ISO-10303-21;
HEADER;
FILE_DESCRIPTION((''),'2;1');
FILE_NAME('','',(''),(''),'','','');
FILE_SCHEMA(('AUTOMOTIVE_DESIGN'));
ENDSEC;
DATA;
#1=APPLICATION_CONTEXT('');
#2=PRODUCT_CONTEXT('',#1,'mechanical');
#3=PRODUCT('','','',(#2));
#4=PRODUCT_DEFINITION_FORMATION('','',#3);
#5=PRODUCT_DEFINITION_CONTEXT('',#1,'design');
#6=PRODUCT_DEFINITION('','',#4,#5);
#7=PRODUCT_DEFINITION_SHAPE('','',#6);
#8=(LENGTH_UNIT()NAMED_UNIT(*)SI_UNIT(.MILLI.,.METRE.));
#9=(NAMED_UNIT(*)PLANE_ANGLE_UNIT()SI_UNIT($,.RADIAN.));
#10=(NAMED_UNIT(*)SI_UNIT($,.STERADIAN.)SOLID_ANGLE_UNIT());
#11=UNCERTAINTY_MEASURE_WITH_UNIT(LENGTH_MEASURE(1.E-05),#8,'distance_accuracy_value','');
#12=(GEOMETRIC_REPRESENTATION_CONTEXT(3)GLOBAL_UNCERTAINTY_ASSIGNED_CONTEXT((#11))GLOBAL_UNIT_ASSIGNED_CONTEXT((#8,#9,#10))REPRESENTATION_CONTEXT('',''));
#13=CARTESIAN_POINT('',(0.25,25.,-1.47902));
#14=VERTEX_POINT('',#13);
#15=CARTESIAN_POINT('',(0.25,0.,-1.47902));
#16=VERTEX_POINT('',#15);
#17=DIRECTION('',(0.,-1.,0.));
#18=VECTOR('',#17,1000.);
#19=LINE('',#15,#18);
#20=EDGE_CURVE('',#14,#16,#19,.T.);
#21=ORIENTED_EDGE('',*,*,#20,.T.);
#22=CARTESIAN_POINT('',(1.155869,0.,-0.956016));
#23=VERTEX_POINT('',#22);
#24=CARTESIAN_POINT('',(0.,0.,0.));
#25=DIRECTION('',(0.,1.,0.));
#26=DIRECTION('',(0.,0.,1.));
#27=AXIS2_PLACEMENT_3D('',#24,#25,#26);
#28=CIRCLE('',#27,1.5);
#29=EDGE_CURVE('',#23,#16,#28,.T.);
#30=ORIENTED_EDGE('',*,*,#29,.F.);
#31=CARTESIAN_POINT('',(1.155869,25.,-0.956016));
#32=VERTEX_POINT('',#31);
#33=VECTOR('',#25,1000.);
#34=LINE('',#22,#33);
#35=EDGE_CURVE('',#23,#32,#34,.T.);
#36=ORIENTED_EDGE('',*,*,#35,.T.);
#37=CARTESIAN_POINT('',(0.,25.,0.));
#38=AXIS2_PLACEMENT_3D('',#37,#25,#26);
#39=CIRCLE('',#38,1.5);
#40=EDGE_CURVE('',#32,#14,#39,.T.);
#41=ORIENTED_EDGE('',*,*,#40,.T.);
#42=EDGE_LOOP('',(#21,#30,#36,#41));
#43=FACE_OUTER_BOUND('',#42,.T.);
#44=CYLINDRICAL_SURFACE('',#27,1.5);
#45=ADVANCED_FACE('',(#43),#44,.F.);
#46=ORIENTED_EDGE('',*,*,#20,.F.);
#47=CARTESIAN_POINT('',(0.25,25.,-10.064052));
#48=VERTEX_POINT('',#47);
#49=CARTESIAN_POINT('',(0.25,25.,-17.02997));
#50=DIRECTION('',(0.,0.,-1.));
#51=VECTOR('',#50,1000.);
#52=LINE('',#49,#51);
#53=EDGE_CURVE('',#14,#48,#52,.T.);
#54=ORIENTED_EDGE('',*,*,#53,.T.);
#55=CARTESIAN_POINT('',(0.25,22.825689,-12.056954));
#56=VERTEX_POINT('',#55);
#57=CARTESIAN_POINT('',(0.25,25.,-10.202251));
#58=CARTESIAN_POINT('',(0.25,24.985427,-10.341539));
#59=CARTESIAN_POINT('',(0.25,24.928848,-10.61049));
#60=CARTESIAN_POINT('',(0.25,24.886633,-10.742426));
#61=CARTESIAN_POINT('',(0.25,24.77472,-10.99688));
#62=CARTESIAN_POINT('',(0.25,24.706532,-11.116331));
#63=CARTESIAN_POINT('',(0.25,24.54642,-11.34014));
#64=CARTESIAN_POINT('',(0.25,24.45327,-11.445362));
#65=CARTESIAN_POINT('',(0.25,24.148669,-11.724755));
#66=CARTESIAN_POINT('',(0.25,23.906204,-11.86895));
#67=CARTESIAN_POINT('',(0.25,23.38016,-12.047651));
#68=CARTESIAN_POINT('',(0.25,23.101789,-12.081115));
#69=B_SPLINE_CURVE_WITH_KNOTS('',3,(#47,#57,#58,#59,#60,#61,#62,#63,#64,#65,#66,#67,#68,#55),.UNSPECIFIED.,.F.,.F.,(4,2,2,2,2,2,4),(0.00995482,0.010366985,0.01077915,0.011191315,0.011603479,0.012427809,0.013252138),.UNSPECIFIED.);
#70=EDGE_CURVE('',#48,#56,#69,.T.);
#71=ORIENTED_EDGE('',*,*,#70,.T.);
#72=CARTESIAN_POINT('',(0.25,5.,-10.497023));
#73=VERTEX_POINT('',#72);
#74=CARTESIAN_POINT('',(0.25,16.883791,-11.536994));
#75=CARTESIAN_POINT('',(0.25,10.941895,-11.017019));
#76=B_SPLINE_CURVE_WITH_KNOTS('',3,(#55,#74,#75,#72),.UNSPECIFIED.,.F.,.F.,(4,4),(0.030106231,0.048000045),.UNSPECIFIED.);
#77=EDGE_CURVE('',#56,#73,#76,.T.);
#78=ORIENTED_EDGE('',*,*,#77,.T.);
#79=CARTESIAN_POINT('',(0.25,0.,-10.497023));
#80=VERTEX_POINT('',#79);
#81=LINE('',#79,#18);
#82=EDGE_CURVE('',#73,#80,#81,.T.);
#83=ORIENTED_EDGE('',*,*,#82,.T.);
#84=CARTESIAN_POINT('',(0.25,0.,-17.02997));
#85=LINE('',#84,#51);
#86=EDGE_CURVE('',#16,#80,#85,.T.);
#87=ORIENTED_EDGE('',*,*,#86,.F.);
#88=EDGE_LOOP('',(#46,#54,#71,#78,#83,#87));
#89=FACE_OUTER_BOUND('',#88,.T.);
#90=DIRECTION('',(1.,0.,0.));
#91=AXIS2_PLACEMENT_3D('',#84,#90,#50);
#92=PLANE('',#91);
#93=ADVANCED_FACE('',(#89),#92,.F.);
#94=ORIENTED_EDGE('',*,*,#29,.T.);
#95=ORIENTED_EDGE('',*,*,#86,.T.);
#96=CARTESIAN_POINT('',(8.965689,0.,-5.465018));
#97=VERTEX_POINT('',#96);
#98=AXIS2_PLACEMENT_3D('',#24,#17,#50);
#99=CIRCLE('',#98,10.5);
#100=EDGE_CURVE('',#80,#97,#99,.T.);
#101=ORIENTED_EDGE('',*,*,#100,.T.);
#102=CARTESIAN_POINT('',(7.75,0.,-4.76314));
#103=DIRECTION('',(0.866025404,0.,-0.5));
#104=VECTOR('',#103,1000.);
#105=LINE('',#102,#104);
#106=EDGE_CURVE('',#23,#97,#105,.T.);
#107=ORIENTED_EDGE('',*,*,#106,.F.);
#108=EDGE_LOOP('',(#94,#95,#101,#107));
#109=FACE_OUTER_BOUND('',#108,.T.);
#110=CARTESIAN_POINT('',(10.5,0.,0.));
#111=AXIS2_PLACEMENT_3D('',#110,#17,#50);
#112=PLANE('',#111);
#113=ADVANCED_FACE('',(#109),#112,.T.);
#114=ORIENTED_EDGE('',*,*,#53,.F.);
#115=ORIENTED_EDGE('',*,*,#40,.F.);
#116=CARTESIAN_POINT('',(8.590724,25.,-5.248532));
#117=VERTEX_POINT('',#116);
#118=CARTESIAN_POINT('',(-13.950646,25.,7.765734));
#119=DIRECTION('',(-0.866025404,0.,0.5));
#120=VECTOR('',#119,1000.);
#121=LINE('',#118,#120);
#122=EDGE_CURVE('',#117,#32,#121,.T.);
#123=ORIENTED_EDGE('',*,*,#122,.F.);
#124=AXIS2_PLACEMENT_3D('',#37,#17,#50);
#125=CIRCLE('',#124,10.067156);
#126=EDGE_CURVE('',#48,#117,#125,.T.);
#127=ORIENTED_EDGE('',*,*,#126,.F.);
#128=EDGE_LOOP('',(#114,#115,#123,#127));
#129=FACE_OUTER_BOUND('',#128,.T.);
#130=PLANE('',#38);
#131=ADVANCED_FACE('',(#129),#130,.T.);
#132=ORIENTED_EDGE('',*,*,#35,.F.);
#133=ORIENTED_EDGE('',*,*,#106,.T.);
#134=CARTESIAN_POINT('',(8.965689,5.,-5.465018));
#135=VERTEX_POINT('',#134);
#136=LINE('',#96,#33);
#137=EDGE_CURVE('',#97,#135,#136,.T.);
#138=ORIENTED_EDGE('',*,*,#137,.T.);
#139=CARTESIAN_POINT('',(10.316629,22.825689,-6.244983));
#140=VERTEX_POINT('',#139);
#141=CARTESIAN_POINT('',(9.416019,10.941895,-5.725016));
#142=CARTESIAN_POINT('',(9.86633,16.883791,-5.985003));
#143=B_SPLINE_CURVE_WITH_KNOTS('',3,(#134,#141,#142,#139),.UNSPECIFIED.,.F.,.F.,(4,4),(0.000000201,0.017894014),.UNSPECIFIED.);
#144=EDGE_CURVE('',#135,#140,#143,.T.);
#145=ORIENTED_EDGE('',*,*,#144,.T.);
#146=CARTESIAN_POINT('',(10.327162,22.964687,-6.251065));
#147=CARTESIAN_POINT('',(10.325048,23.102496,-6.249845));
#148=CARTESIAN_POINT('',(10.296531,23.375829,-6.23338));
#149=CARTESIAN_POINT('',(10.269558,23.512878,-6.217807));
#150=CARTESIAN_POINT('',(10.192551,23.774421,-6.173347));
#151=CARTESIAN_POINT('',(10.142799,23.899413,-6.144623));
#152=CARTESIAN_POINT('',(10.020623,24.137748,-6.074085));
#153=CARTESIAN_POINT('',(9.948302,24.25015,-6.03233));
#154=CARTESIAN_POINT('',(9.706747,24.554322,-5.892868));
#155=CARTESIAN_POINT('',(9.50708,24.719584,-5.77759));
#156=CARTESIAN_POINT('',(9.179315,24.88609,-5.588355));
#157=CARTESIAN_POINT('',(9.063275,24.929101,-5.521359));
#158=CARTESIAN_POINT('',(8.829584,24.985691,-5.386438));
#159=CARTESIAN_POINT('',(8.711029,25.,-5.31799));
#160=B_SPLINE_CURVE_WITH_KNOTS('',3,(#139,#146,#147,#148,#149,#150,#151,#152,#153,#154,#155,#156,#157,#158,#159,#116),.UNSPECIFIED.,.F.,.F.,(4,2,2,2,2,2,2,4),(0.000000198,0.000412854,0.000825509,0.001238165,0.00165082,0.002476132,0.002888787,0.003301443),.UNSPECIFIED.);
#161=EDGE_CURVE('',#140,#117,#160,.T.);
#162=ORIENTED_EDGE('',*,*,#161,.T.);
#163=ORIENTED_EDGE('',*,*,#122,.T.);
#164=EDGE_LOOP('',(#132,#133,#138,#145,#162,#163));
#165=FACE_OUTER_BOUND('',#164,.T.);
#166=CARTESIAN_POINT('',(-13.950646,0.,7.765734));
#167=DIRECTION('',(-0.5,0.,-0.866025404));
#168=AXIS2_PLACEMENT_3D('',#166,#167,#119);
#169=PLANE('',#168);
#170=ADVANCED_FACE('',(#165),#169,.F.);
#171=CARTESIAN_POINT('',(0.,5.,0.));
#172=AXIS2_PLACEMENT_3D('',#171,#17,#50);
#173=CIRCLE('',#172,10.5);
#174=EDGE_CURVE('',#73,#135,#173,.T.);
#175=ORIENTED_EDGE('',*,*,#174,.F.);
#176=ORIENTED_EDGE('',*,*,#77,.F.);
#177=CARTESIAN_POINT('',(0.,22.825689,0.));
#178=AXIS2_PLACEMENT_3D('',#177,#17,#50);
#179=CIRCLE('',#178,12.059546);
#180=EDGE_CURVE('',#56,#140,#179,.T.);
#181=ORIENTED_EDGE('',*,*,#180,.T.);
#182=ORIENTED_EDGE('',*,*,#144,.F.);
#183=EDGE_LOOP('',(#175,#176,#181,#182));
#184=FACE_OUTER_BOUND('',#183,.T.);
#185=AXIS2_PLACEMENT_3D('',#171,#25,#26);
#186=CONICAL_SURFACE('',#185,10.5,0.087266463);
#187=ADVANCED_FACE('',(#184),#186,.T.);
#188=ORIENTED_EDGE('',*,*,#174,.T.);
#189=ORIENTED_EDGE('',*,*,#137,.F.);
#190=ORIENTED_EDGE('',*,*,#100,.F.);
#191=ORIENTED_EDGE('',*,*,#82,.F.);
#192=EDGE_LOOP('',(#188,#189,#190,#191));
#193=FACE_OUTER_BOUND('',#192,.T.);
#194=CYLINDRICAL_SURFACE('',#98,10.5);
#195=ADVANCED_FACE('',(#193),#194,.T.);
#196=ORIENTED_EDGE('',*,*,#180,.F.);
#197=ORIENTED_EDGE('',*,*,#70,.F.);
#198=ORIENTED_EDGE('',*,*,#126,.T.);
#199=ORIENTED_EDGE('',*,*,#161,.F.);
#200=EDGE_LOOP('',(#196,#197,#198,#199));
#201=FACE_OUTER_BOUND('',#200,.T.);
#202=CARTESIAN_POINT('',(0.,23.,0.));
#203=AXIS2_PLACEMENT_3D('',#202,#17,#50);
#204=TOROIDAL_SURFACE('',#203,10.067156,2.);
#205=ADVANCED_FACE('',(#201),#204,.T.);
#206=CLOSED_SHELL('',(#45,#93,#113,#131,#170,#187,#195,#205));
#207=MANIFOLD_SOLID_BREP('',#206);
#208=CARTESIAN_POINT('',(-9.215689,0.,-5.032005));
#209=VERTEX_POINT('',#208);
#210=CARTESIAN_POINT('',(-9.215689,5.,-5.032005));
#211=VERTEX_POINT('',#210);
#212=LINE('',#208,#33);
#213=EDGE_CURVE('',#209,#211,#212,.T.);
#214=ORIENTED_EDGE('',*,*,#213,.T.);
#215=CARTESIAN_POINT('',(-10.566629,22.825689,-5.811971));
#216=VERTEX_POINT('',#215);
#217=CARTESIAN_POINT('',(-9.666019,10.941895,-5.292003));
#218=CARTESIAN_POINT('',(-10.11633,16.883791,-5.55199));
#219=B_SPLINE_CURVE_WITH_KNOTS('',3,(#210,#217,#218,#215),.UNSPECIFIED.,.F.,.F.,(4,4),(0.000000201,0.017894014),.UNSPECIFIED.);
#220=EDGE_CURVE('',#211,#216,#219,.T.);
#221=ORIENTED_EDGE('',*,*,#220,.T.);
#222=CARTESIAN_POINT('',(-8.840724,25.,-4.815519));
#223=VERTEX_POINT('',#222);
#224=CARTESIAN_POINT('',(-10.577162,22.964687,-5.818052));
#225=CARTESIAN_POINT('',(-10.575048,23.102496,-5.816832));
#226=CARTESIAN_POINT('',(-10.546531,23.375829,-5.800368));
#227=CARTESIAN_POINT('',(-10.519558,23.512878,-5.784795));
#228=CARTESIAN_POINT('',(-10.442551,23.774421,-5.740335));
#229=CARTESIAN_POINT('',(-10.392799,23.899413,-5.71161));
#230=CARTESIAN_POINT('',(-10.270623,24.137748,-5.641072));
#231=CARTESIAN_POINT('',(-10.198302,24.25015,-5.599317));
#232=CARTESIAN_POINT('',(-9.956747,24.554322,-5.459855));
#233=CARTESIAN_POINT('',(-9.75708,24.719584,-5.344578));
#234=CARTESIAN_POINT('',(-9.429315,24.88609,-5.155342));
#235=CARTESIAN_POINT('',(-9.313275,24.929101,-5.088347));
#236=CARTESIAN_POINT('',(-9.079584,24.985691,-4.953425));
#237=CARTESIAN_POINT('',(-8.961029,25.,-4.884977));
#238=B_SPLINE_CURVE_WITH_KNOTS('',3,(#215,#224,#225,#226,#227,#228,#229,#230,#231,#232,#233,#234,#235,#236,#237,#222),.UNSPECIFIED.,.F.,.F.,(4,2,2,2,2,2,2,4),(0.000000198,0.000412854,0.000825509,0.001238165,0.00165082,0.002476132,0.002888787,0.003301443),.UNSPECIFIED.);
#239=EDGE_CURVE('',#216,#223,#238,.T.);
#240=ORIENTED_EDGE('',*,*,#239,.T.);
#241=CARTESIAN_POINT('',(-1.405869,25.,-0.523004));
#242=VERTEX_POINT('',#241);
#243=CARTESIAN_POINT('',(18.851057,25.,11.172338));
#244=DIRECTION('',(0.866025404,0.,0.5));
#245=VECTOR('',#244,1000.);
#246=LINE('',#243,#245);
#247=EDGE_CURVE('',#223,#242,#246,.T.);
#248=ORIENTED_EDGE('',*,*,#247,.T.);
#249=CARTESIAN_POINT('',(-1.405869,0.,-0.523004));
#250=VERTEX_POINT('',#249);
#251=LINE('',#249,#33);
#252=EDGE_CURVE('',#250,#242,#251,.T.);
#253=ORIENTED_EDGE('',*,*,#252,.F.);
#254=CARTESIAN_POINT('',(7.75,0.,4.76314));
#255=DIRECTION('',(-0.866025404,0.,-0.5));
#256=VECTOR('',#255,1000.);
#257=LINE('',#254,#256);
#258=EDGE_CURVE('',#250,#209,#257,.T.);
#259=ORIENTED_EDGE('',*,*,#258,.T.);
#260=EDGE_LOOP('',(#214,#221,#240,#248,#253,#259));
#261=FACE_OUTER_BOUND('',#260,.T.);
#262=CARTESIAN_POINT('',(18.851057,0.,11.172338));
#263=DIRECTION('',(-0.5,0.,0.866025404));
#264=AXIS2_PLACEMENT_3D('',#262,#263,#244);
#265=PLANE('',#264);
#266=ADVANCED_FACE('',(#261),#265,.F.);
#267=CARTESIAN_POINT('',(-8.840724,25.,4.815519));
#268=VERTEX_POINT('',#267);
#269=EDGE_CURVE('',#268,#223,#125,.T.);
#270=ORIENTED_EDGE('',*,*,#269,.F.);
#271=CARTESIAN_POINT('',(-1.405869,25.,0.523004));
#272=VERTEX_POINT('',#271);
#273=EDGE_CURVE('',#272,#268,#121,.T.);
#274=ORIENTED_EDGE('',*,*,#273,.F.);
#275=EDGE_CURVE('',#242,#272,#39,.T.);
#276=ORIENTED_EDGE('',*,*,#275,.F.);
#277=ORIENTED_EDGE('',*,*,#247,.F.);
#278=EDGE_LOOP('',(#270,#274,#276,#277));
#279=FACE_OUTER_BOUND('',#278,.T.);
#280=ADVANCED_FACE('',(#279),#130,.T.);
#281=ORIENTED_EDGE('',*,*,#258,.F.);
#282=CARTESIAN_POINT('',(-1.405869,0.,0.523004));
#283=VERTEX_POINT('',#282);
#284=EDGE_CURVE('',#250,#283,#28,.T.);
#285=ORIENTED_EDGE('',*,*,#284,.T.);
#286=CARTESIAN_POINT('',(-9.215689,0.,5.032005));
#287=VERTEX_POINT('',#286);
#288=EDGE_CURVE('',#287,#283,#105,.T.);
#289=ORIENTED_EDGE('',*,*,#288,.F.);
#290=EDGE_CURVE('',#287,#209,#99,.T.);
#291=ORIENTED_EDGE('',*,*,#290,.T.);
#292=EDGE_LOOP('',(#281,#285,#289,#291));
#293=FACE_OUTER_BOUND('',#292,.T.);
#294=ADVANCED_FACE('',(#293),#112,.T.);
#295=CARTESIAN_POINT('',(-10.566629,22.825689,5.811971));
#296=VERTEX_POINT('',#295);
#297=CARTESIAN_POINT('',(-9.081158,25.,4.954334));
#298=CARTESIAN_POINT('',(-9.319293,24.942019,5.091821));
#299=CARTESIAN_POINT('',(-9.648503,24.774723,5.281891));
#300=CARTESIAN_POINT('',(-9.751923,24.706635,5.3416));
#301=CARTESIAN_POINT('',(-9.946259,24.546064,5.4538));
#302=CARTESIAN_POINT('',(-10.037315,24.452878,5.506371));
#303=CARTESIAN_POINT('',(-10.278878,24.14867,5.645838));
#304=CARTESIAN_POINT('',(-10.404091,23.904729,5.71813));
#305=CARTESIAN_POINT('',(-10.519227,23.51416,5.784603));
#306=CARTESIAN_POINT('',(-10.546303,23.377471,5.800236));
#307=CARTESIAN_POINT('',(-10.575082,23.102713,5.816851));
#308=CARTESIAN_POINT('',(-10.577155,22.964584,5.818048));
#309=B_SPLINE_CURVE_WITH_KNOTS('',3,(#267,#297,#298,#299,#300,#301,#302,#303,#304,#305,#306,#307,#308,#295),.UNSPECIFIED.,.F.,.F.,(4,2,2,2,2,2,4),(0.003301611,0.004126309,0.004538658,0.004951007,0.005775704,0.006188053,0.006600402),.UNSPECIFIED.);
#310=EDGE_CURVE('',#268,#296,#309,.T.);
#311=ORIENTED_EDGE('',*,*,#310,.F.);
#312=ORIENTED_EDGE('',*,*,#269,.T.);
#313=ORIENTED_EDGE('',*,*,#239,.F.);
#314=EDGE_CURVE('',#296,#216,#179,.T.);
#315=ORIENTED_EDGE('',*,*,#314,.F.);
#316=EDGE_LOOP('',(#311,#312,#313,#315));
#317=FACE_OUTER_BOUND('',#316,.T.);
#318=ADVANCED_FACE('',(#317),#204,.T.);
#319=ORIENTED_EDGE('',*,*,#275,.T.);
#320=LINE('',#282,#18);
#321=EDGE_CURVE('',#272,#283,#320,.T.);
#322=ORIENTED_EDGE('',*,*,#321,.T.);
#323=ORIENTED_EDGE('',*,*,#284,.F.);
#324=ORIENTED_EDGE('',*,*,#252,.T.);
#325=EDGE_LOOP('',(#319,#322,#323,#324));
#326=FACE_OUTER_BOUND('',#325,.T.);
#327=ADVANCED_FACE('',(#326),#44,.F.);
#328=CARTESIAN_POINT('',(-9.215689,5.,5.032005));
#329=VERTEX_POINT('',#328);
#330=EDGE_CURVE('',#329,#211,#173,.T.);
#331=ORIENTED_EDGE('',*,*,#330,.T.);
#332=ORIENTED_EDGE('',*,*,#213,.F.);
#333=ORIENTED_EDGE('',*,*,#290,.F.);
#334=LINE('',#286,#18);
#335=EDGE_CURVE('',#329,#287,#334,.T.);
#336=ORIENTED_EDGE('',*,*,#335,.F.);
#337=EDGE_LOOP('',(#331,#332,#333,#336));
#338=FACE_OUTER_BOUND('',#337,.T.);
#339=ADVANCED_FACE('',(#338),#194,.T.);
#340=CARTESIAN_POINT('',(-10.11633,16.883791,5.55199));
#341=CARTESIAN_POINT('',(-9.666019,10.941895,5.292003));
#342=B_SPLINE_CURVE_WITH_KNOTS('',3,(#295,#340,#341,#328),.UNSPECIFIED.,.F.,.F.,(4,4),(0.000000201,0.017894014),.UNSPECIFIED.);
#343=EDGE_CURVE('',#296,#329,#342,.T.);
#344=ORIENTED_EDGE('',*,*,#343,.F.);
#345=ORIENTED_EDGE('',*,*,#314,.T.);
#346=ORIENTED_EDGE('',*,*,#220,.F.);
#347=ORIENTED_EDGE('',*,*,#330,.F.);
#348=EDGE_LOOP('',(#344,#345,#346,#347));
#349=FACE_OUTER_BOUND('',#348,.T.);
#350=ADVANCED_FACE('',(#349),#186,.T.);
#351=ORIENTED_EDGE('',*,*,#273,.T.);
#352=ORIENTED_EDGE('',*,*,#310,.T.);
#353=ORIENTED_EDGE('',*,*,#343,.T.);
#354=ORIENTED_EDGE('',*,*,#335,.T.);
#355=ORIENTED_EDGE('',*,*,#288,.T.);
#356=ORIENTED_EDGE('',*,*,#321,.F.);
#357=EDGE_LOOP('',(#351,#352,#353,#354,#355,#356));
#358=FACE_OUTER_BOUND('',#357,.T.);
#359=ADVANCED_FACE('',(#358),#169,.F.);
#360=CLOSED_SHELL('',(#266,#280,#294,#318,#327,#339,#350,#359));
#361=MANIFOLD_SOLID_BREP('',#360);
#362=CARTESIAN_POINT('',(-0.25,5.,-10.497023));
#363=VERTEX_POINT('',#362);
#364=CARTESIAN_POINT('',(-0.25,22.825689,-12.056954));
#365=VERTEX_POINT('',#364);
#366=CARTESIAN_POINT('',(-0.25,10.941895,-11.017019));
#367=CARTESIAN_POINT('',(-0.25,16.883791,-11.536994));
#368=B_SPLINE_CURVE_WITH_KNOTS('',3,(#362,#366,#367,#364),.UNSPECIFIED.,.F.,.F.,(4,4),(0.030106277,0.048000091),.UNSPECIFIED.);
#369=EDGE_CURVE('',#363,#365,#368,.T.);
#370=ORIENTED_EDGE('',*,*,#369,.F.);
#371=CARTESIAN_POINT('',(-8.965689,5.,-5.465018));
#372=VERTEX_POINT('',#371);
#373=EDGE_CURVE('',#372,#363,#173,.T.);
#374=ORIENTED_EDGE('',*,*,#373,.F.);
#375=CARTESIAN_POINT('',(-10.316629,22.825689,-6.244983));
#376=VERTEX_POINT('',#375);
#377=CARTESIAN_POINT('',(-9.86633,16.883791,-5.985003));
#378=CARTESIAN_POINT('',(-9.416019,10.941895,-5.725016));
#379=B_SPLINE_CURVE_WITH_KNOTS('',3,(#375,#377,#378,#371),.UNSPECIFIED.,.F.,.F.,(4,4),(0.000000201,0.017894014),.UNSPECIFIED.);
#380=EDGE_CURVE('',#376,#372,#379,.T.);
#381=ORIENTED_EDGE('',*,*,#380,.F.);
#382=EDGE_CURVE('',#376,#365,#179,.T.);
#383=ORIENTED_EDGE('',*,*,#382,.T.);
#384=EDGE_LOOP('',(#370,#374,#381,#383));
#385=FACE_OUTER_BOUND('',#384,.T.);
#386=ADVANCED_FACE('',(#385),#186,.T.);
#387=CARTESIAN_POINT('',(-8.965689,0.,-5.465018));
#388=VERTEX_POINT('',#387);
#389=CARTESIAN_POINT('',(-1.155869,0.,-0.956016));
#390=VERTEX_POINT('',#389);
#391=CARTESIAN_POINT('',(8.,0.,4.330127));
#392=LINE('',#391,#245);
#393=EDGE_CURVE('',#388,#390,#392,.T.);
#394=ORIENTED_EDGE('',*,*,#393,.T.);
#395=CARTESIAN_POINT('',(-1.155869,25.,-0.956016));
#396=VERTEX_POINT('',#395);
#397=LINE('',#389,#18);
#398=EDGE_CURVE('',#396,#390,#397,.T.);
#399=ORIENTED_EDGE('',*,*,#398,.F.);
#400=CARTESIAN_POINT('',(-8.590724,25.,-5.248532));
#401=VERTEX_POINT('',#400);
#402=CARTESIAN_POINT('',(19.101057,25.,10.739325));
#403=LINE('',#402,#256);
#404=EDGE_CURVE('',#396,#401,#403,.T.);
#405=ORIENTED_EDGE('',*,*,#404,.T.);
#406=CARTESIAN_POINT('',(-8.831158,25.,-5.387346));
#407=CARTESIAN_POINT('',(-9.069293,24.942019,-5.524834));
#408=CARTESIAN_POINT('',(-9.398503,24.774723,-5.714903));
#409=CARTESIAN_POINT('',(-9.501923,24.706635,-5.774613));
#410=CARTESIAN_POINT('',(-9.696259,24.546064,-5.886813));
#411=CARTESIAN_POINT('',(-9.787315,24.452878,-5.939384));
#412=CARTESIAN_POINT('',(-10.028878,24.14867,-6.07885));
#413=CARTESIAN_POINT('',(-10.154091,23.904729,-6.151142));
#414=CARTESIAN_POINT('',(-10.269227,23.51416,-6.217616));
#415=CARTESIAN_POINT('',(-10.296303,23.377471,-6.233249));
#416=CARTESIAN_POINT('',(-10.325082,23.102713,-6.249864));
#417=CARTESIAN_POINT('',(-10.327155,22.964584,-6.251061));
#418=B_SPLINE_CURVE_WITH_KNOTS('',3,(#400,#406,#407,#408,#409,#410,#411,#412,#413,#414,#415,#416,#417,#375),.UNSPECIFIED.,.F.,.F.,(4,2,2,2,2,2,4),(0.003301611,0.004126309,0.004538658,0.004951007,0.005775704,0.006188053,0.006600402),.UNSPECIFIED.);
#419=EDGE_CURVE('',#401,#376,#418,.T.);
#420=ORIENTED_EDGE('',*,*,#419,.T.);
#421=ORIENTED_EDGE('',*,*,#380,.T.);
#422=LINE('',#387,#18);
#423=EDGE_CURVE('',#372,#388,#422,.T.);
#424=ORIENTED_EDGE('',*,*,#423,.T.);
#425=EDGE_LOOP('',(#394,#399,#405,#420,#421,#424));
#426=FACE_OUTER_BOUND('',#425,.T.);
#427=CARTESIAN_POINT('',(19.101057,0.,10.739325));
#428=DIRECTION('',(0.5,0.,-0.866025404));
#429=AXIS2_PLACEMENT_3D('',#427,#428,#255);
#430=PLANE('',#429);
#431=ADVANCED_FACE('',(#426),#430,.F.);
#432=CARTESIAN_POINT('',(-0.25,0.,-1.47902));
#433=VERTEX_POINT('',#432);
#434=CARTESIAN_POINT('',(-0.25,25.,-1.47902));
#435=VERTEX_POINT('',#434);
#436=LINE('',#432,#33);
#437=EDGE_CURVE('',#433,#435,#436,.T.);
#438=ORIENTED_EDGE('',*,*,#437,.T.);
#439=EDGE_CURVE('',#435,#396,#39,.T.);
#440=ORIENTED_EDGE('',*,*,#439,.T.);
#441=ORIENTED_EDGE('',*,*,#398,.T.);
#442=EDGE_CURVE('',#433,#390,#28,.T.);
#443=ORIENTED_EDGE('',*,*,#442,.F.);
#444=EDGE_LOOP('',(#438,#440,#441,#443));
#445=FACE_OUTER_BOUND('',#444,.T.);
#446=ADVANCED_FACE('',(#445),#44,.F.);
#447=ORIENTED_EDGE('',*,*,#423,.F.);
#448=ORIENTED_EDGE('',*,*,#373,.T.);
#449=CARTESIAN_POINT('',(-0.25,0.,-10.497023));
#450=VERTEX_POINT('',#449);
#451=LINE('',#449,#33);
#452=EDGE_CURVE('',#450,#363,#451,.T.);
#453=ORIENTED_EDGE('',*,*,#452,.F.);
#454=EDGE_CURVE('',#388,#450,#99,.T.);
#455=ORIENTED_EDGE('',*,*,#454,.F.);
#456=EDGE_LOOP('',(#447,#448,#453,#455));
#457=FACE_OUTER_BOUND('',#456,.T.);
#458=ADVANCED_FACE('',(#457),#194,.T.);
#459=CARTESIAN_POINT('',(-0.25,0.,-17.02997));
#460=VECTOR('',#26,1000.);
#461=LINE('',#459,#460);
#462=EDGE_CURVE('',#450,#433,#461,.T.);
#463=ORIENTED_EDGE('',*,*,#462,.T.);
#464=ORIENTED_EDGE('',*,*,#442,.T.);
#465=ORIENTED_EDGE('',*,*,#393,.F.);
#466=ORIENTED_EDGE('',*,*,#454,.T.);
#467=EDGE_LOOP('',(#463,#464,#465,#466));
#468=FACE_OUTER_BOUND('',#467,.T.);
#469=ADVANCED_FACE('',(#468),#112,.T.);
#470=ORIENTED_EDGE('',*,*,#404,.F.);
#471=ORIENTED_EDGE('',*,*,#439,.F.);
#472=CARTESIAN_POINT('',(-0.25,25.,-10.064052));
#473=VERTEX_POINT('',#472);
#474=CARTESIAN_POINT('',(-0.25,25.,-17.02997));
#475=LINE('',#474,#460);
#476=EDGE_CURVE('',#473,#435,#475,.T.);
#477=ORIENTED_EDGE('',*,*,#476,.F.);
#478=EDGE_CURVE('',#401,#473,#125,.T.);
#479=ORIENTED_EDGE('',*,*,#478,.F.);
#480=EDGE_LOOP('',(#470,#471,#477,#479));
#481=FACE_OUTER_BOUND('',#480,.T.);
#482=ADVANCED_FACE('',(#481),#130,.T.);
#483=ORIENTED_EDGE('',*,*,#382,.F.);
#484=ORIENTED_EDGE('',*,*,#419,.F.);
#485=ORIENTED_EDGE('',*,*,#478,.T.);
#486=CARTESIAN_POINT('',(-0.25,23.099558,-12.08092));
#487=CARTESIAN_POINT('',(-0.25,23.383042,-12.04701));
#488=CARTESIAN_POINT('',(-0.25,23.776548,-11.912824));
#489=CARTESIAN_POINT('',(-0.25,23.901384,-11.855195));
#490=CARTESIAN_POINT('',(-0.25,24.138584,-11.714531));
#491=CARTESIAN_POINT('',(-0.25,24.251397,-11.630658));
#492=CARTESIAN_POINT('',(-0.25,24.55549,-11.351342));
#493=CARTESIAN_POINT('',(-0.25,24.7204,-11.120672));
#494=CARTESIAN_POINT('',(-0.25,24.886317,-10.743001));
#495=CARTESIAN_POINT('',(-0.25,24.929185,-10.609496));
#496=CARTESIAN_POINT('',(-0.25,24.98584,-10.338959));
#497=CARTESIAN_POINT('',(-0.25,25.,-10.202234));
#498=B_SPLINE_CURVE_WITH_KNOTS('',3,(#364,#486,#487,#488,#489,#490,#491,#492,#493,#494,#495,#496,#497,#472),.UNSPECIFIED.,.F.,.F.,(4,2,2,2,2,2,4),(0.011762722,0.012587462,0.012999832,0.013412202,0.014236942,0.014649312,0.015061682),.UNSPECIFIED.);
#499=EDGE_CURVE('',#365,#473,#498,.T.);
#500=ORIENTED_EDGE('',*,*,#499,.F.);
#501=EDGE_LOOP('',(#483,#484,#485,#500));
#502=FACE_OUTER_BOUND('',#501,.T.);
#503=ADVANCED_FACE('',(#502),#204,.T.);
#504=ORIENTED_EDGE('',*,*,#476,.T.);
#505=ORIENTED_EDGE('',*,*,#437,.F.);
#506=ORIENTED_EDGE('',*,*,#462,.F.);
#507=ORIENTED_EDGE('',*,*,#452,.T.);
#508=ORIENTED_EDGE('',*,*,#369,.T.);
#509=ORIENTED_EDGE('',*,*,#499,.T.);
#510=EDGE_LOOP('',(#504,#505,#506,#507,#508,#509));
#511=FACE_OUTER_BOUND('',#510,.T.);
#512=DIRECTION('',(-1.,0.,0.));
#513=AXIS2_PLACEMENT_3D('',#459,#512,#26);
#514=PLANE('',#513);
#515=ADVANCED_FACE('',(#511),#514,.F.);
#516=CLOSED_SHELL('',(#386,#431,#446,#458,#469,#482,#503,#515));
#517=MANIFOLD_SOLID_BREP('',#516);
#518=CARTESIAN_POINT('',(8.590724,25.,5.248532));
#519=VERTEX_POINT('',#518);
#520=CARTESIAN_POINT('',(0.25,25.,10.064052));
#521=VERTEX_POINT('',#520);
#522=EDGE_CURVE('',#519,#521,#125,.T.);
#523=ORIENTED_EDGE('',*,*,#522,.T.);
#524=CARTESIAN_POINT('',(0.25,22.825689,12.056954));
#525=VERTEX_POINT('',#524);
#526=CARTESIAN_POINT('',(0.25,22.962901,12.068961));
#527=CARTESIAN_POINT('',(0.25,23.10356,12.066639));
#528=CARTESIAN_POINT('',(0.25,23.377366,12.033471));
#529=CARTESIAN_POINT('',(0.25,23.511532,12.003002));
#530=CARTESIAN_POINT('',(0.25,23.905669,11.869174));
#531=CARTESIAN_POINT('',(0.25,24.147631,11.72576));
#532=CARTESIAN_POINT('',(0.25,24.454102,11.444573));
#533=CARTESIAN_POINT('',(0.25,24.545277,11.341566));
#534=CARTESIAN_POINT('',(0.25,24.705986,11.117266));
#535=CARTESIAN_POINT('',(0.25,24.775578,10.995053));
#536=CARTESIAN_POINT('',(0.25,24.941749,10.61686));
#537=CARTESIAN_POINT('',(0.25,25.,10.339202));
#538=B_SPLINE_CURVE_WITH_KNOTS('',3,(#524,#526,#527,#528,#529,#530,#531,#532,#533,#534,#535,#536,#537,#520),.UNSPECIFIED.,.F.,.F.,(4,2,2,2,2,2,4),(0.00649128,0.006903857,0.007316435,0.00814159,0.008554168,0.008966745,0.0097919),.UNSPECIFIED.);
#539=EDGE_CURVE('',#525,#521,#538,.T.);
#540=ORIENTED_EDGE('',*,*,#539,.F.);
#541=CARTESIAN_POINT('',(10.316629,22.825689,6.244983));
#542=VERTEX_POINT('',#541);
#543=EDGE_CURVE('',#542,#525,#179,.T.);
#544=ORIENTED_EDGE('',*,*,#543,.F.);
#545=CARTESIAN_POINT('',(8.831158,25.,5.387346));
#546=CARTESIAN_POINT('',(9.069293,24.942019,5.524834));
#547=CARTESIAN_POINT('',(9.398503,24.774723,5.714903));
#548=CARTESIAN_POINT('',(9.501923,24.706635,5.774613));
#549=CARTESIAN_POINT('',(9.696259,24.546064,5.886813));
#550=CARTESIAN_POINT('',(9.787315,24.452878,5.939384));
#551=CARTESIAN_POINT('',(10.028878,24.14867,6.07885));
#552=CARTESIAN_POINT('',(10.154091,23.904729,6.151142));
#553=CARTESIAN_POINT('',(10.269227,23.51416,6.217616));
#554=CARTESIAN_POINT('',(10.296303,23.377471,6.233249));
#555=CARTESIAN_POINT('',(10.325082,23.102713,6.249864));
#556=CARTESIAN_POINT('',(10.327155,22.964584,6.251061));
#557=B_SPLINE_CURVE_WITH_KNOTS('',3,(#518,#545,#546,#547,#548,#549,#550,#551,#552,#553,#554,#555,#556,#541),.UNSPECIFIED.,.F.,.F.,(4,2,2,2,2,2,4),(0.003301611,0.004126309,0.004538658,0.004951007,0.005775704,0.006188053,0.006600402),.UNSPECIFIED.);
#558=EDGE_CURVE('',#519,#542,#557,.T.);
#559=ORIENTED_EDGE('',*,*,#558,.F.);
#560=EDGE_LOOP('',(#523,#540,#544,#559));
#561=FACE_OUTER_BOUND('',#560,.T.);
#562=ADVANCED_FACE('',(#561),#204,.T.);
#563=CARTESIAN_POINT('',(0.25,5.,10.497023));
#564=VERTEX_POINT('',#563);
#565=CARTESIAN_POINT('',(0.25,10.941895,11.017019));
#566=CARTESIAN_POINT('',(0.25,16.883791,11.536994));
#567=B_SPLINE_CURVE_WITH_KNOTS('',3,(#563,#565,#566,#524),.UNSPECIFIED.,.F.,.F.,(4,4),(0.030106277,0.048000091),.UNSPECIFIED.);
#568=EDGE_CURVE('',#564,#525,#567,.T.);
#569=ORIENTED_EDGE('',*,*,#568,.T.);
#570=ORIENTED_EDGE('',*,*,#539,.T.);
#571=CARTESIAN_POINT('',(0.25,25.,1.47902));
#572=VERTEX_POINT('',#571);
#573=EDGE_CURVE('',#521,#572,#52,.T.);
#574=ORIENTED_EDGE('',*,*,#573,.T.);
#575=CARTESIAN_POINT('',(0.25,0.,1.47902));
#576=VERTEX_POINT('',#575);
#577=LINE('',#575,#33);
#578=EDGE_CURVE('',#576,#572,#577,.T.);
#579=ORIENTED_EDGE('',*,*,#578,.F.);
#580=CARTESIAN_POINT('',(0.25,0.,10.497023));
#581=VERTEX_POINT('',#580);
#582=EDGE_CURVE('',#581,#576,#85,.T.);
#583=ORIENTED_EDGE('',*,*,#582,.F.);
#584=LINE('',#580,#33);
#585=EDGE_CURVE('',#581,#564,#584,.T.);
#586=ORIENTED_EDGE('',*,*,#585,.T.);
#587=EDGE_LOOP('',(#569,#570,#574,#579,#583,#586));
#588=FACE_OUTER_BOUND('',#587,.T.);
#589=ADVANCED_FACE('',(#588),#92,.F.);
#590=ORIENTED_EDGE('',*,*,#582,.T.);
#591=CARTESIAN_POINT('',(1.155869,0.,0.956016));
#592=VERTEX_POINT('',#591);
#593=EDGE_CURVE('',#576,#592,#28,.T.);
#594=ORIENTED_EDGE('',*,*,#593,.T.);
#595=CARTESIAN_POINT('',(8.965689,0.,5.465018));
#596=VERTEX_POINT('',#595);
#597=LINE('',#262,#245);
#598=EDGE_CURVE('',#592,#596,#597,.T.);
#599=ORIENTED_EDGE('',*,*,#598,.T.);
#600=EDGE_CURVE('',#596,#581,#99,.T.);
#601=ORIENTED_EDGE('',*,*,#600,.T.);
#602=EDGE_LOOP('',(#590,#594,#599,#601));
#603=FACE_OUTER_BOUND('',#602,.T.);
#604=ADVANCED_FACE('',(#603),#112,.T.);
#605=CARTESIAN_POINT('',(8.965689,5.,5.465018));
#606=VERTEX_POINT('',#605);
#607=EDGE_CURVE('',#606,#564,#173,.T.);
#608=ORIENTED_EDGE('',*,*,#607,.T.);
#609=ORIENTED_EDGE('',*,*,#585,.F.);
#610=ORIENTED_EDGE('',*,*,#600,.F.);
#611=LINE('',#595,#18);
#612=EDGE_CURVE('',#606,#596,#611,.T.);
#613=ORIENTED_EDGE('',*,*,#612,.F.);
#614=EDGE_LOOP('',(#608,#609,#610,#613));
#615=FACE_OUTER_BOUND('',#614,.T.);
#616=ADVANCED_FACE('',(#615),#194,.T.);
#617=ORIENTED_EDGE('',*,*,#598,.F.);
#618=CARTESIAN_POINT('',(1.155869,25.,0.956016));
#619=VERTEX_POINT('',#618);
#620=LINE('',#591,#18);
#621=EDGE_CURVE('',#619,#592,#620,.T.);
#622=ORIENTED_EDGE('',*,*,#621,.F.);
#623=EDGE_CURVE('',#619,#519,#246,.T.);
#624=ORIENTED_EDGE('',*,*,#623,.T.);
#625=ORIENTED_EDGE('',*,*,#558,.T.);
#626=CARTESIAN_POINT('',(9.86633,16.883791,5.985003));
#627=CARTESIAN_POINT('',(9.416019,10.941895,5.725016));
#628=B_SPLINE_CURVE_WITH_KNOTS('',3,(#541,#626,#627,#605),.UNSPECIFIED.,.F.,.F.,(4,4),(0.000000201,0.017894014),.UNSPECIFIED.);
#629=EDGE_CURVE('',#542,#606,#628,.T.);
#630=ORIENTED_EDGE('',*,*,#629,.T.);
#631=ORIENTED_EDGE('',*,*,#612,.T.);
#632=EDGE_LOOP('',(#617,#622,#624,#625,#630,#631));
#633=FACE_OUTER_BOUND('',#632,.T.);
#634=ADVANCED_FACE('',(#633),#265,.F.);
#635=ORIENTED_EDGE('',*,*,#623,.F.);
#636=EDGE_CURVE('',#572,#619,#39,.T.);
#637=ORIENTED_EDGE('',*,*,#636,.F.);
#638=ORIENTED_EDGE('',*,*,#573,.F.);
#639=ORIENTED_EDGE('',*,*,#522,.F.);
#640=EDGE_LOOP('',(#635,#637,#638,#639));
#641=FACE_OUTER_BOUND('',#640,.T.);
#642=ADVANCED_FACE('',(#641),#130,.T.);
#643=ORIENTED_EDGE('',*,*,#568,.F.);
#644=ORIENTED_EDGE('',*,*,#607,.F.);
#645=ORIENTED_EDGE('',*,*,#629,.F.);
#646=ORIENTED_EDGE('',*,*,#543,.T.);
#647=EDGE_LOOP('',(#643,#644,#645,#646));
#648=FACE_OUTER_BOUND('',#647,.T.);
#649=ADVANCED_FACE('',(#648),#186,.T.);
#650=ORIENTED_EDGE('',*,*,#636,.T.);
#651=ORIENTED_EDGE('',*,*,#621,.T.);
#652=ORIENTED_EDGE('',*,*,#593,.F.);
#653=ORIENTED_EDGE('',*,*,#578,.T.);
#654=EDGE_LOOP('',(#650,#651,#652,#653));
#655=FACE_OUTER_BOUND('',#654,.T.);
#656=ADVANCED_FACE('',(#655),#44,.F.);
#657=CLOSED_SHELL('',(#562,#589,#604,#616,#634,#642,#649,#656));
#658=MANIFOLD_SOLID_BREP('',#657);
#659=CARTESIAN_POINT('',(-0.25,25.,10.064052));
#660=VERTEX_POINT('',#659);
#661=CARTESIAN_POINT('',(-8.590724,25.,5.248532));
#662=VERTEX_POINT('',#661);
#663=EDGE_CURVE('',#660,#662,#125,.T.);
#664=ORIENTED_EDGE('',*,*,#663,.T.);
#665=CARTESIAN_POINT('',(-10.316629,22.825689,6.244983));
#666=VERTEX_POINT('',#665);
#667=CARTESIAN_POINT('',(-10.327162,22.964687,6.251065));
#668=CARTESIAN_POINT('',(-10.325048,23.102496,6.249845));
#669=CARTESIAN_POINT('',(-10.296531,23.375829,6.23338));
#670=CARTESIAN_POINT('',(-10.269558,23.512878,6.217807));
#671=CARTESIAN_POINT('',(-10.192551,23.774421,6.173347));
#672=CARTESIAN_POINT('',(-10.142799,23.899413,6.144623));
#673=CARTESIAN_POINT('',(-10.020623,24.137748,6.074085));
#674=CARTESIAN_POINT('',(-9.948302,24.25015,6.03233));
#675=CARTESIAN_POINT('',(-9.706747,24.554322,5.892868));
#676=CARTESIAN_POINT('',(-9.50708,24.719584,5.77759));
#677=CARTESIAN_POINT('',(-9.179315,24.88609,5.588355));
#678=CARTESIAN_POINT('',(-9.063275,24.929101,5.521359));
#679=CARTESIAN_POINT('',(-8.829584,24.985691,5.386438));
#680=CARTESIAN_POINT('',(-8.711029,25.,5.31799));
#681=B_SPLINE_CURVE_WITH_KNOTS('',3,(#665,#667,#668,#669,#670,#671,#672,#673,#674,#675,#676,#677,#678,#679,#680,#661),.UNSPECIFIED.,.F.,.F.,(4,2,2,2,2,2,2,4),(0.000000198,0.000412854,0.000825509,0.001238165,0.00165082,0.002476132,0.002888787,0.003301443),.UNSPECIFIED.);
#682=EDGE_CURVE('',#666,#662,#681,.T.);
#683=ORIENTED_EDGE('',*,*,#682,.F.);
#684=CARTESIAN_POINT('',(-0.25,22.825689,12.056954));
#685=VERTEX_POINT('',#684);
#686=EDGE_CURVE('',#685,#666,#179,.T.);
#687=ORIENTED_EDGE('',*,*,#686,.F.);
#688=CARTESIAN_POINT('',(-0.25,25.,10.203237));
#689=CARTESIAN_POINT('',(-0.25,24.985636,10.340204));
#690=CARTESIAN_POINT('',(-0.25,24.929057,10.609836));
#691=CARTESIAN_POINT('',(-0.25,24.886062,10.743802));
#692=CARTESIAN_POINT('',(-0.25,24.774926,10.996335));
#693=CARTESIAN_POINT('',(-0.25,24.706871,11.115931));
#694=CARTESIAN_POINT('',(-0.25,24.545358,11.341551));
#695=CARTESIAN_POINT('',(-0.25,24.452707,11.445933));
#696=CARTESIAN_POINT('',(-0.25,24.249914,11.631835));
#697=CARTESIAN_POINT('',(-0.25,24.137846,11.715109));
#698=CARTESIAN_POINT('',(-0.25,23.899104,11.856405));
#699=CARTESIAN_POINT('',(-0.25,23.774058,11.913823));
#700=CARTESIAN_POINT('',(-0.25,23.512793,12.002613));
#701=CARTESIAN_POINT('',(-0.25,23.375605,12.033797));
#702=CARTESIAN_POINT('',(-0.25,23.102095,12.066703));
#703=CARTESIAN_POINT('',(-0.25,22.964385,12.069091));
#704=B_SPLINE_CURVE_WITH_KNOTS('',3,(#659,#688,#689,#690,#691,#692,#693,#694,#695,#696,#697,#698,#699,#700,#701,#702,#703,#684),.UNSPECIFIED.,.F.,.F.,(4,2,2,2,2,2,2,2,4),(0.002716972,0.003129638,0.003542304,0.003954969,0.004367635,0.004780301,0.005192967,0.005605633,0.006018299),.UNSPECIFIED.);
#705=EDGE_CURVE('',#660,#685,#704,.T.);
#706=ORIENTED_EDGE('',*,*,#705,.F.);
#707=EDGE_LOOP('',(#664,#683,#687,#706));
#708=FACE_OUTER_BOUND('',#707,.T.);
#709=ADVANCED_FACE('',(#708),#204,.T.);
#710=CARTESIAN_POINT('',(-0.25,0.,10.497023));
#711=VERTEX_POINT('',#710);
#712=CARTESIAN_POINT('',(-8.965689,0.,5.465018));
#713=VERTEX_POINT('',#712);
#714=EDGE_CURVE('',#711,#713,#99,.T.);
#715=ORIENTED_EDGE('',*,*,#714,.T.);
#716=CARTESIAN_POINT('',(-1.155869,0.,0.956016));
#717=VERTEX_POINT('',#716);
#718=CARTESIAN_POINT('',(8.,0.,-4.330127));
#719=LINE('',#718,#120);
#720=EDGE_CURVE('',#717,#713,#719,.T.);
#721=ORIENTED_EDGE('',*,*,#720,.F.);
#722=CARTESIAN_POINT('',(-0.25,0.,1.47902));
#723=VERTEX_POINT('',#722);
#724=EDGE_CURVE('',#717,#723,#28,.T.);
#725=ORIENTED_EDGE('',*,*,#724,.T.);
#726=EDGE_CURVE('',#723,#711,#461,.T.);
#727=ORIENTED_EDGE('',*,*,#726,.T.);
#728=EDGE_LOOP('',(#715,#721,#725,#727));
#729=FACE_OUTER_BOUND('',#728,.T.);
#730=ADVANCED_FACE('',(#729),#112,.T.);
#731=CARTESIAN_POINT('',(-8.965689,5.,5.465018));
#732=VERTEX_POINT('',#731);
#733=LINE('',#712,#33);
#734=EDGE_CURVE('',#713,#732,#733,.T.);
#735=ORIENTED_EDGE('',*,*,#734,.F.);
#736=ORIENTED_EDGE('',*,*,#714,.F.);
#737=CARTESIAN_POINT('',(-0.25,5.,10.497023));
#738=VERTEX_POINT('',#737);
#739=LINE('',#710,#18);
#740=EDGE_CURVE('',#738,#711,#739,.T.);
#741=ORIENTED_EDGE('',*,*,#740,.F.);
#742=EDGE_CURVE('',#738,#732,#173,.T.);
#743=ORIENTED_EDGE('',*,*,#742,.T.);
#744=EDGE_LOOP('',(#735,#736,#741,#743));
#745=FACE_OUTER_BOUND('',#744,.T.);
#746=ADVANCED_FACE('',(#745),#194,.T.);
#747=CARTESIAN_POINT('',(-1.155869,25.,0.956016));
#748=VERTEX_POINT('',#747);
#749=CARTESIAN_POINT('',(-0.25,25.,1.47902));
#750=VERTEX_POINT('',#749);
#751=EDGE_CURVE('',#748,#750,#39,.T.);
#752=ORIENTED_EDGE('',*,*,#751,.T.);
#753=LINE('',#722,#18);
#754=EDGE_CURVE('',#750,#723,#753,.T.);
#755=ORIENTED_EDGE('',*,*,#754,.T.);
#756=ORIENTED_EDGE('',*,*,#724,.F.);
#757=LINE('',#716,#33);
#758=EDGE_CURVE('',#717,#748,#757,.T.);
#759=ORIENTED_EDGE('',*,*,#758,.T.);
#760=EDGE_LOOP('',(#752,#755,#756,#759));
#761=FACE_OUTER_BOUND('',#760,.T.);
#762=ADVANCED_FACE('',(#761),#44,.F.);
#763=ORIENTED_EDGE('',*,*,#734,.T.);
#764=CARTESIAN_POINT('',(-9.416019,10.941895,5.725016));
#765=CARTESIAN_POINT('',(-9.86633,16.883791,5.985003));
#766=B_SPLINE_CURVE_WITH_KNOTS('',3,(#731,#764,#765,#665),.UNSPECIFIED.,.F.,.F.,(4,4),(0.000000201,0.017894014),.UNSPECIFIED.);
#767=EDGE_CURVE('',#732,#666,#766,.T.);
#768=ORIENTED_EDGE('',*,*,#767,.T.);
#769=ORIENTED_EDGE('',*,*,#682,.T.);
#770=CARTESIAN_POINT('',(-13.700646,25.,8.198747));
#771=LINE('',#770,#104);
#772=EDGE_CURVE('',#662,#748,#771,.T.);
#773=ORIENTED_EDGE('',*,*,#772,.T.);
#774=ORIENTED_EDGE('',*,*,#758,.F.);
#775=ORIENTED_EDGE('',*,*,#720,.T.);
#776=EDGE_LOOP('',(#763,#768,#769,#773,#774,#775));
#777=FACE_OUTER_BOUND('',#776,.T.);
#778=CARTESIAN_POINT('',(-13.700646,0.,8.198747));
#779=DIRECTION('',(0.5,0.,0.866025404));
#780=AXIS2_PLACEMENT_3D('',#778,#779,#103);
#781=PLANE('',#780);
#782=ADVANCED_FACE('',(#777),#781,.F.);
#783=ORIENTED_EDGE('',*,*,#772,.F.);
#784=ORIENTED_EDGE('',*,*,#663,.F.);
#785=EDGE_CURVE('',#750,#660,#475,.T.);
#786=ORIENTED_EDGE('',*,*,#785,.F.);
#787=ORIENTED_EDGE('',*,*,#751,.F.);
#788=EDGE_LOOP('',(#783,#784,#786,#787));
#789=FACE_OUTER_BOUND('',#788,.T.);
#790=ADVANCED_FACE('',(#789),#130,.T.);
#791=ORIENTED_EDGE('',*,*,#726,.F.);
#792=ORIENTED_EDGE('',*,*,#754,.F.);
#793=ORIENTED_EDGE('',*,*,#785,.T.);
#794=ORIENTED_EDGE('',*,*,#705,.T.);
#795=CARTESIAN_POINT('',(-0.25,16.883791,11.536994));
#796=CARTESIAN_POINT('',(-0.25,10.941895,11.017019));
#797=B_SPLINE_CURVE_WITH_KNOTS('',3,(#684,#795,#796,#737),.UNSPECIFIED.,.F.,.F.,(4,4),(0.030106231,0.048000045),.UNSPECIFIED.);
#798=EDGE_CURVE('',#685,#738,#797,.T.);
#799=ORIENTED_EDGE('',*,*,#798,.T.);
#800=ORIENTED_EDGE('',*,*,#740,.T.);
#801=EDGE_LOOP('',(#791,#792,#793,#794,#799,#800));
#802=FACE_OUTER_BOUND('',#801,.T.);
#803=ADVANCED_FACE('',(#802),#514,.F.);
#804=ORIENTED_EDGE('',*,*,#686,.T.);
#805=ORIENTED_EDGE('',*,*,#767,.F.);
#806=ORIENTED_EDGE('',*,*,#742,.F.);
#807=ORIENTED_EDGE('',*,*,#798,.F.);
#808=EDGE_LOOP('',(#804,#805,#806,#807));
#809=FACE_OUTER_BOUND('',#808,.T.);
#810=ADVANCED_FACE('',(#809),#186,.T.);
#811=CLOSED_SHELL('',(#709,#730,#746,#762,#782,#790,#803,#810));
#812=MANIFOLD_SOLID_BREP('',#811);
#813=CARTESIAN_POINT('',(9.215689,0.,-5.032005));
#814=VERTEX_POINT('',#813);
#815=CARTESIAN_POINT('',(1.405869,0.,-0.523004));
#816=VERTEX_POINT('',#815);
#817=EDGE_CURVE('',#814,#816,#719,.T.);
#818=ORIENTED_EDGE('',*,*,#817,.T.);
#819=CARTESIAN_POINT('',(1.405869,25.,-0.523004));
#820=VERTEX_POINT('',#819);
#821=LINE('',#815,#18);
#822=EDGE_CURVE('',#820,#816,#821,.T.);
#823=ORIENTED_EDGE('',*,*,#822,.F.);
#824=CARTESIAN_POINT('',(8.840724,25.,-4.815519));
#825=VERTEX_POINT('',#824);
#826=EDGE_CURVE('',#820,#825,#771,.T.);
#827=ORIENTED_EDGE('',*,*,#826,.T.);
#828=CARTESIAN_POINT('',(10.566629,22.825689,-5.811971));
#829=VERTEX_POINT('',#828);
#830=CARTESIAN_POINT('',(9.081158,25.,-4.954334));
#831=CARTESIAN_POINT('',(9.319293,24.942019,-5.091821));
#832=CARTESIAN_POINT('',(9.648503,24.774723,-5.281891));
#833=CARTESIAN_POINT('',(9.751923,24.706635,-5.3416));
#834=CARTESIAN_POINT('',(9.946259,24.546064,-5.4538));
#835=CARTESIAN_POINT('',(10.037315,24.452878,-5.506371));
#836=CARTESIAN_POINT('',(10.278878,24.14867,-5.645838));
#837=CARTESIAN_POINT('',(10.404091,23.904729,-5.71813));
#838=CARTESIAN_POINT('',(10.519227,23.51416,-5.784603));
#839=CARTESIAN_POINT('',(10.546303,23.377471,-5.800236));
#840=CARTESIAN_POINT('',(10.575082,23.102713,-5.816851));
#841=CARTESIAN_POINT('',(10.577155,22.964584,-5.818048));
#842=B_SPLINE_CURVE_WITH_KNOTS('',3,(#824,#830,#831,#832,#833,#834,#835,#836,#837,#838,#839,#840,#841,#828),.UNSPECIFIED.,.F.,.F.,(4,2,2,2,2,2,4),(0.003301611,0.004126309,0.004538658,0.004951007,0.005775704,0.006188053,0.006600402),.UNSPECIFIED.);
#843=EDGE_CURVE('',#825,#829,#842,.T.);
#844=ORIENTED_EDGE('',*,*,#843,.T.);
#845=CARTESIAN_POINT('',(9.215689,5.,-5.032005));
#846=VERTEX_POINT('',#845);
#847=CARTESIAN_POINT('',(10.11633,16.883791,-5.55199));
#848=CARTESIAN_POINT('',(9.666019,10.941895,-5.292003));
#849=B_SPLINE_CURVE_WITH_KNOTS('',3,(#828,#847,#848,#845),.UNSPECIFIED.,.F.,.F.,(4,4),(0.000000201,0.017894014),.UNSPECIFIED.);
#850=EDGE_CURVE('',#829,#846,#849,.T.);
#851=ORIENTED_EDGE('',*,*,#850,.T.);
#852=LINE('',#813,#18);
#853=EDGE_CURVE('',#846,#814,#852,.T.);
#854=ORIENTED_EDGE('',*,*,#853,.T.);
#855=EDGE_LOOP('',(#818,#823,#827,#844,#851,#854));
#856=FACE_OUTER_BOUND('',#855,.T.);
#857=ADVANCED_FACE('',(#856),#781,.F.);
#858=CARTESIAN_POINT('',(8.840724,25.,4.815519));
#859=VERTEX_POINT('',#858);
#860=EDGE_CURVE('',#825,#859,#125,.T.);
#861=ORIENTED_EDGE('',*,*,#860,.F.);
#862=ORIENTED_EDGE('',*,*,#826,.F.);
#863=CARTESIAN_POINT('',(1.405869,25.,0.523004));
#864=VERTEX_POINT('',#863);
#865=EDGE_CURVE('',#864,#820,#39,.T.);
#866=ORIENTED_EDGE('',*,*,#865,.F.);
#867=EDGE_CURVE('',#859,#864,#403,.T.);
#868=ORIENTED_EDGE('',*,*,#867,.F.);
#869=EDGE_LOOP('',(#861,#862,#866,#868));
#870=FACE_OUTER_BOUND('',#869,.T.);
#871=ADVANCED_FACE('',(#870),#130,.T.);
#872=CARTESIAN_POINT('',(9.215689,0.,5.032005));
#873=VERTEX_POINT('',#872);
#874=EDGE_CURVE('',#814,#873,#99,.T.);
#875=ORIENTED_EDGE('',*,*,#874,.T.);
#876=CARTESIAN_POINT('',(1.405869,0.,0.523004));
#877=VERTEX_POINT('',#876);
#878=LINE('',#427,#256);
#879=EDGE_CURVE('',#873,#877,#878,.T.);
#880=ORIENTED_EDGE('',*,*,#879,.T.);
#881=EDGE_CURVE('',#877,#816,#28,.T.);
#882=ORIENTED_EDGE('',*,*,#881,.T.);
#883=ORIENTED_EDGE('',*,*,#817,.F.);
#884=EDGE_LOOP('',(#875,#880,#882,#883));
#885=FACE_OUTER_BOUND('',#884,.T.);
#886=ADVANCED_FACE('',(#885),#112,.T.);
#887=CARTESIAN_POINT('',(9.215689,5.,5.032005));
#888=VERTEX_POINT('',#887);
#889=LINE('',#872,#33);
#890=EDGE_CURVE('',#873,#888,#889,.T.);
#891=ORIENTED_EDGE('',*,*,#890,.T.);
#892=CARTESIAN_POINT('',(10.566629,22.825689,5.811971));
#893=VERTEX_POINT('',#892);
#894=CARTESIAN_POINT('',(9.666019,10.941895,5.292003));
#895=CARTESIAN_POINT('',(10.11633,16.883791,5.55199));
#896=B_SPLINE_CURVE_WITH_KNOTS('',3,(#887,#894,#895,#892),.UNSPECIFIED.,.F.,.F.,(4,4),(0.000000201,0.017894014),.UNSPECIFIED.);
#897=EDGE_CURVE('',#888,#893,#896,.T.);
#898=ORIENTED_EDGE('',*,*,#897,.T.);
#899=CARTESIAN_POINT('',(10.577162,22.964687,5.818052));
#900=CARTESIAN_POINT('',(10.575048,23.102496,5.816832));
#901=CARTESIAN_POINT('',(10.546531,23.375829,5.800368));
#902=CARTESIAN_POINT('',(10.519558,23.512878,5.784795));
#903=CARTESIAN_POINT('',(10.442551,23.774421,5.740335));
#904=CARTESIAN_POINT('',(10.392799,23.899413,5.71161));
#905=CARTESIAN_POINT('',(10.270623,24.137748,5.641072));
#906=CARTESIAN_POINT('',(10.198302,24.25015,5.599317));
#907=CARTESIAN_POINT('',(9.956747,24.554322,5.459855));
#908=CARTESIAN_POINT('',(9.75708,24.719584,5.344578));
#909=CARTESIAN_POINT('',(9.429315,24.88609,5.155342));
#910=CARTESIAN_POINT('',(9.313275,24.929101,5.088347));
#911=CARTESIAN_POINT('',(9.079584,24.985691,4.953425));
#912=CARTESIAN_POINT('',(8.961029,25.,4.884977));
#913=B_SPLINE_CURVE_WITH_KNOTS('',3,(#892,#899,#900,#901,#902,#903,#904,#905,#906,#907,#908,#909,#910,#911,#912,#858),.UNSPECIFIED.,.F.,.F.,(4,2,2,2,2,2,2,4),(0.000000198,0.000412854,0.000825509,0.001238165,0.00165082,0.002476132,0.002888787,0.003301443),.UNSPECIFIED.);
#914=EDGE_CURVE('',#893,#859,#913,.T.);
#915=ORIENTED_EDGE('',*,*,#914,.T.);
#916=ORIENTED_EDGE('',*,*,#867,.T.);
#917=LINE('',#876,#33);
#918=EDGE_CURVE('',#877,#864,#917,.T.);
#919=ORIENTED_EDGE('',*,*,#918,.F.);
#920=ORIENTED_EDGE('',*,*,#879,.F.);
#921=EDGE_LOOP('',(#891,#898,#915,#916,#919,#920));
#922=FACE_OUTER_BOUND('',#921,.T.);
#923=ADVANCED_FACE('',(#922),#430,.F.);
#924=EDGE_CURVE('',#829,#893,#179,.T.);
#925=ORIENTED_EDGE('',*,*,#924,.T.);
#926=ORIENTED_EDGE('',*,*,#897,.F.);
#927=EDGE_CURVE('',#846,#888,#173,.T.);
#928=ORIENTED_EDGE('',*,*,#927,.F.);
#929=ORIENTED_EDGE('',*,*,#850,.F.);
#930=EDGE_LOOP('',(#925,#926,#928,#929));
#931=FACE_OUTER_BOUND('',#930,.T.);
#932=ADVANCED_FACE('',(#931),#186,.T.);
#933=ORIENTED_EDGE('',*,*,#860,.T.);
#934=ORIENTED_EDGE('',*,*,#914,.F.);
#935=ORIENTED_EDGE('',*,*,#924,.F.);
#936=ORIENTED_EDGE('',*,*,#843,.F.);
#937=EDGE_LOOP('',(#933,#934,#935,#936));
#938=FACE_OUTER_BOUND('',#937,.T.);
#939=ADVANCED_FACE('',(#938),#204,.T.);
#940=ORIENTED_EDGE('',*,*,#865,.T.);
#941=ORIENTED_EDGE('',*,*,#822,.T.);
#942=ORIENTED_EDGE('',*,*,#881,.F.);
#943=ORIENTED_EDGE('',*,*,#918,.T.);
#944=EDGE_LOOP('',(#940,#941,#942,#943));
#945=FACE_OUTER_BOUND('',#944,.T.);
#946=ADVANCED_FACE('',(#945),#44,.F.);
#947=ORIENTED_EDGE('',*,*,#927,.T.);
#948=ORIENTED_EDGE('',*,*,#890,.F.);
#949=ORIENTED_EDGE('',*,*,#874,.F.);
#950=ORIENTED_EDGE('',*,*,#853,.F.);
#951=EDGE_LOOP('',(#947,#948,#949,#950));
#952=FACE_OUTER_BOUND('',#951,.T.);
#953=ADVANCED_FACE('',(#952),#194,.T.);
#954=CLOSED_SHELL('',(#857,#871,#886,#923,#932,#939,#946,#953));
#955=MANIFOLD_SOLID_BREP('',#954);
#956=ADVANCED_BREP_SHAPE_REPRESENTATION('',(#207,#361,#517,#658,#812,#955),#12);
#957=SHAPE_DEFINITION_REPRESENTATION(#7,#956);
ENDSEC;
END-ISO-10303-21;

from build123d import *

# Parameters (mm, degrees)
SKETCH_2_R          = 1.5
CUT_EXTRUDE_1_DEPTH = 31.269333089
SKETCH_3_W          = 0.5
SKETCH_3_H          = 34.059940126
CUT_EXTRUDE_2_DEPTH = 31.269333089
CUT_EXTRUDE_3_DEPTH = 31.268300756
CUT_EXTRUDE_4_DEPTH = 31.268300756


with BuildPart() as part:
    # 草图1 → 旋转1 (revolve)
    with BuildSketch(Plane.XY, mode=Mode.PRIVATE) as revolve_1_sk:
        with BuildLine():
            Line((0, 25), (10.067156268, 25))
            ThreePointArc((10.067156268, 25), (11.541710942, 24.351180415), (12.059545665, 22.825688515))
            Line((12.059545665, 22.825688515), (10.5, 5))
            Line((10.5, 5), (10.5, 0))
            Line((10.5, 0), (0, 0))
            Line((0, 0), (0, 25))
        make_face()
    revolve(revolve_1_sk.sketch.rotate(Axis((0, 0, 0), (0, 1, 0)), 90), axis=Axis((0, 0, 0), (0, 1, 0)))

    # 草图2 → 切除-拉伸1 (cut, through all)
    with BuildSketch(Plane(origin=(0, 25, 0), x_dir=(1, 0, 0), z_dir=(0, 1, 0))):
        with Locations(Location((0, 0, 0), (0, 0, 270))):
            Circle(SKETCH_2_R)
    extrude(amount=-CUT_EXTRUDE_1_DEPTH, mode=Mode.SUBTRACT)

    # 草图3 → 切除-拉伸2 (cut, through all)
    with BuildSketch(Plane(origin=(0, 25, 0), x_dir=(1, 0, 0), z_dir=(0, 1, 0))):
        Rectangle(SKETCH_3_W, SKETCH_3_H)
    extrude(amount=-CUT_EXTRUDE_2_DEPTH, mode=Mode.SUBTRACT)


with BuildPart() as cut_extrude_2_piece_1:
    # of the separate pieces the step leaves, piece 1, a body of its own (cut_extrude_2_pieces)
    add(part.part.solids().sort_by_distance((0.25, 25, -10.064051636))[0])


with BuildPart() as cut_extrude_2_piece_2:
    # of the separate pieces the step leaves, piece 2, a body of its own (cut_extrude_2_pieces)
    add(part.part.solids().sort_by_distance((-0.25, 25, -10.064051636))[0])


with BuildPart() as cut_extrude_3_tool:
    # 草图4 → 切除-拉伸3 (new, through all)
    with BuildSketch(Plane(origin=(0, 25, 0), x_dir=(1, 0, 0), z_dir=(0, 1, 0))):
        Polygon((18.851057357, -11.172338174), (19.101057357, -10.739325472), (-18.851057357, 11.172338174), (-19.101057357, 10.739325472), align=None)
    extrude(amount=-CUT_EXTRUDE_3_DEPTH)


with BuildPart() as cut_extrude_2_piece_1_1:
    add(cut_extrude_2_piece_1.part)

    # 切除-拉伸3: cut by cut_extrude_3_tool
    add(cut_extrude_3_tool.part, mode=Mode.SUBTRACT)


with BuildPart() as cut_extrude_2_piece_2_1:
    add(cut_extrude_2_piece_2.part)

    # 切除-拉伸3: cut by cut_extrude_3_tool
    add(cut_extrude_3_tool.part, mode=Mode.SUBTRACT)


with BuildPart() as cut_extrude_3_piece_1:
    # of the separate pieces the step leaves, piece 1, a body of its own (cut_extrude_3_pieces)
    add(cut_extrude_2_piece_1_1.part.solids().sort_by_distance((0.25, 25, -10.064051636))[0])


with BuildPart() as cut_extrude_3_piece_2:
    # of the separate pieces the step leaves, piece 2, a body of its own (cut_extrude_3_pieces)
    add(cut_extrude_2_piece_1_1.part.solids().sort_by_distance((1.155868846, 25, 0.956016324))[0])


with BuildPart() as cut_extrude_3_piece_1_of_cut_extrude_2_p:
    # of the separate pieces the step leaves, piece 1, a body of its own (cut_extrude_3_pieces_of_cut_extrude_2_pi)
    add(cut_extrude_2_piece_2_1.part.solids().sort_by_distance((-8.840724382, 25, -4.815519467))[0])


with BuildPart() as cut_extrude_3_piece_2_of_cut_extrude_2_p:
    # of the separate pieces the step leaves, piece 2, a body of its own (cut_extrude_3_pieces_of_cut_extrude_2_pi)
    add(cut_extrude_2_piece_2_1.part.solids().sort_by_distance((-0.25, 25, -10.064051636))[0])


with BuildPart() as cut_extrude_4_tool:
    # 草图5 → 切除-拉伸4 (new, through all)
    with BuildSketch(Plane(origin=(0, 25, 0), x_dir=(1, 0, 0), z_dir=(0, 1, 0))):
        Polygon((-13.95064617, -7.765734187), (-13.70064617, -8.198746889), (13.95064617, 7.765734187), (13.70064617, 8.198746889), align=None)
    extrude(amount=-CUT_EXTRUDE_4_DEPTH)


with BuildPart() as cut_extrude_3_piece_1_1:
    add(cut_extrude_3_piece_1.part)

    # 切除-拉伸4: cut by cut_extrude_4_tool
    add(cut_extrude_4_tool.part, mode=Mode.SUBTRACT)


with BuildPart() as cut_extrude_3_piece_1_of_cut_extrude_2_p_1:
    add(cut_extrude_3_piece_1_of_cut_extrude_2_p.part)

    # 切除-拉伸4: cut by cut_extrude_4_tool
    add(cut_extrude_4_tool.part, mode=Mode.SUBTRACT)


with BuildPart() as cut_extrude_4_piece_1:
    # of the separate pieces the step leaves, piece 1, a body of its own (cut_extrude_4_pieces)
    add(cut_extrude_3_piece_1_1.part.solids().sort_by_distance((1.405868846, 25, -0.523003622))[0])


with BuildPart() as cut_extrude_4_piece_2:
    # of the separate pieces the step leaves, piece 2, a body of its own (cut_extrude_4_pieces)
    add(cut_extrude_3_piece_1_1.part.solids().sort_by_distance((0.25, 25, -10.064051636))[0])


with BuildPart() as cut_extrude_4_piece_1_of_cut_extrude_3_p:
    # of the separate pieces the step leaves, piece 1, a body of its own (cut_extrude_4_pieces_of_cut_extrude_3_pi)
    add(cut_extrude_3_piece_1_of_cut_extrude_2_p_1.part.solids().sort_by_distance((-8.840724382, 25, -4.815519467))[0])


with BuildPart() as cut_extrude_4_piece_2_of_cut_extrude_3_p:
    # of the separate pieces the step leaves, piece 2, a body of its own (cut_extrude_4_pieces_of_cut_extrude_3_pi)
    add(cut_extrude_3_piece_1_of_cut_extrude_2_p_1.part.solids().sort_by_distance((-8.590724382, 25, 5.248532169))[0])


solid = Compound([cut_extrude_3_piece_2.part, cut_extrude_3_piece_2_of_cut_extrude_2_p.part, cut_extrude_4_piece_1.part, cut_extrude_4_piece_2.part, cut_extrude_4_piece_1_of_cut_extrude_3_p.part, cut_extrude_4_piece_2_of_cut_extrude_3_p.part])
